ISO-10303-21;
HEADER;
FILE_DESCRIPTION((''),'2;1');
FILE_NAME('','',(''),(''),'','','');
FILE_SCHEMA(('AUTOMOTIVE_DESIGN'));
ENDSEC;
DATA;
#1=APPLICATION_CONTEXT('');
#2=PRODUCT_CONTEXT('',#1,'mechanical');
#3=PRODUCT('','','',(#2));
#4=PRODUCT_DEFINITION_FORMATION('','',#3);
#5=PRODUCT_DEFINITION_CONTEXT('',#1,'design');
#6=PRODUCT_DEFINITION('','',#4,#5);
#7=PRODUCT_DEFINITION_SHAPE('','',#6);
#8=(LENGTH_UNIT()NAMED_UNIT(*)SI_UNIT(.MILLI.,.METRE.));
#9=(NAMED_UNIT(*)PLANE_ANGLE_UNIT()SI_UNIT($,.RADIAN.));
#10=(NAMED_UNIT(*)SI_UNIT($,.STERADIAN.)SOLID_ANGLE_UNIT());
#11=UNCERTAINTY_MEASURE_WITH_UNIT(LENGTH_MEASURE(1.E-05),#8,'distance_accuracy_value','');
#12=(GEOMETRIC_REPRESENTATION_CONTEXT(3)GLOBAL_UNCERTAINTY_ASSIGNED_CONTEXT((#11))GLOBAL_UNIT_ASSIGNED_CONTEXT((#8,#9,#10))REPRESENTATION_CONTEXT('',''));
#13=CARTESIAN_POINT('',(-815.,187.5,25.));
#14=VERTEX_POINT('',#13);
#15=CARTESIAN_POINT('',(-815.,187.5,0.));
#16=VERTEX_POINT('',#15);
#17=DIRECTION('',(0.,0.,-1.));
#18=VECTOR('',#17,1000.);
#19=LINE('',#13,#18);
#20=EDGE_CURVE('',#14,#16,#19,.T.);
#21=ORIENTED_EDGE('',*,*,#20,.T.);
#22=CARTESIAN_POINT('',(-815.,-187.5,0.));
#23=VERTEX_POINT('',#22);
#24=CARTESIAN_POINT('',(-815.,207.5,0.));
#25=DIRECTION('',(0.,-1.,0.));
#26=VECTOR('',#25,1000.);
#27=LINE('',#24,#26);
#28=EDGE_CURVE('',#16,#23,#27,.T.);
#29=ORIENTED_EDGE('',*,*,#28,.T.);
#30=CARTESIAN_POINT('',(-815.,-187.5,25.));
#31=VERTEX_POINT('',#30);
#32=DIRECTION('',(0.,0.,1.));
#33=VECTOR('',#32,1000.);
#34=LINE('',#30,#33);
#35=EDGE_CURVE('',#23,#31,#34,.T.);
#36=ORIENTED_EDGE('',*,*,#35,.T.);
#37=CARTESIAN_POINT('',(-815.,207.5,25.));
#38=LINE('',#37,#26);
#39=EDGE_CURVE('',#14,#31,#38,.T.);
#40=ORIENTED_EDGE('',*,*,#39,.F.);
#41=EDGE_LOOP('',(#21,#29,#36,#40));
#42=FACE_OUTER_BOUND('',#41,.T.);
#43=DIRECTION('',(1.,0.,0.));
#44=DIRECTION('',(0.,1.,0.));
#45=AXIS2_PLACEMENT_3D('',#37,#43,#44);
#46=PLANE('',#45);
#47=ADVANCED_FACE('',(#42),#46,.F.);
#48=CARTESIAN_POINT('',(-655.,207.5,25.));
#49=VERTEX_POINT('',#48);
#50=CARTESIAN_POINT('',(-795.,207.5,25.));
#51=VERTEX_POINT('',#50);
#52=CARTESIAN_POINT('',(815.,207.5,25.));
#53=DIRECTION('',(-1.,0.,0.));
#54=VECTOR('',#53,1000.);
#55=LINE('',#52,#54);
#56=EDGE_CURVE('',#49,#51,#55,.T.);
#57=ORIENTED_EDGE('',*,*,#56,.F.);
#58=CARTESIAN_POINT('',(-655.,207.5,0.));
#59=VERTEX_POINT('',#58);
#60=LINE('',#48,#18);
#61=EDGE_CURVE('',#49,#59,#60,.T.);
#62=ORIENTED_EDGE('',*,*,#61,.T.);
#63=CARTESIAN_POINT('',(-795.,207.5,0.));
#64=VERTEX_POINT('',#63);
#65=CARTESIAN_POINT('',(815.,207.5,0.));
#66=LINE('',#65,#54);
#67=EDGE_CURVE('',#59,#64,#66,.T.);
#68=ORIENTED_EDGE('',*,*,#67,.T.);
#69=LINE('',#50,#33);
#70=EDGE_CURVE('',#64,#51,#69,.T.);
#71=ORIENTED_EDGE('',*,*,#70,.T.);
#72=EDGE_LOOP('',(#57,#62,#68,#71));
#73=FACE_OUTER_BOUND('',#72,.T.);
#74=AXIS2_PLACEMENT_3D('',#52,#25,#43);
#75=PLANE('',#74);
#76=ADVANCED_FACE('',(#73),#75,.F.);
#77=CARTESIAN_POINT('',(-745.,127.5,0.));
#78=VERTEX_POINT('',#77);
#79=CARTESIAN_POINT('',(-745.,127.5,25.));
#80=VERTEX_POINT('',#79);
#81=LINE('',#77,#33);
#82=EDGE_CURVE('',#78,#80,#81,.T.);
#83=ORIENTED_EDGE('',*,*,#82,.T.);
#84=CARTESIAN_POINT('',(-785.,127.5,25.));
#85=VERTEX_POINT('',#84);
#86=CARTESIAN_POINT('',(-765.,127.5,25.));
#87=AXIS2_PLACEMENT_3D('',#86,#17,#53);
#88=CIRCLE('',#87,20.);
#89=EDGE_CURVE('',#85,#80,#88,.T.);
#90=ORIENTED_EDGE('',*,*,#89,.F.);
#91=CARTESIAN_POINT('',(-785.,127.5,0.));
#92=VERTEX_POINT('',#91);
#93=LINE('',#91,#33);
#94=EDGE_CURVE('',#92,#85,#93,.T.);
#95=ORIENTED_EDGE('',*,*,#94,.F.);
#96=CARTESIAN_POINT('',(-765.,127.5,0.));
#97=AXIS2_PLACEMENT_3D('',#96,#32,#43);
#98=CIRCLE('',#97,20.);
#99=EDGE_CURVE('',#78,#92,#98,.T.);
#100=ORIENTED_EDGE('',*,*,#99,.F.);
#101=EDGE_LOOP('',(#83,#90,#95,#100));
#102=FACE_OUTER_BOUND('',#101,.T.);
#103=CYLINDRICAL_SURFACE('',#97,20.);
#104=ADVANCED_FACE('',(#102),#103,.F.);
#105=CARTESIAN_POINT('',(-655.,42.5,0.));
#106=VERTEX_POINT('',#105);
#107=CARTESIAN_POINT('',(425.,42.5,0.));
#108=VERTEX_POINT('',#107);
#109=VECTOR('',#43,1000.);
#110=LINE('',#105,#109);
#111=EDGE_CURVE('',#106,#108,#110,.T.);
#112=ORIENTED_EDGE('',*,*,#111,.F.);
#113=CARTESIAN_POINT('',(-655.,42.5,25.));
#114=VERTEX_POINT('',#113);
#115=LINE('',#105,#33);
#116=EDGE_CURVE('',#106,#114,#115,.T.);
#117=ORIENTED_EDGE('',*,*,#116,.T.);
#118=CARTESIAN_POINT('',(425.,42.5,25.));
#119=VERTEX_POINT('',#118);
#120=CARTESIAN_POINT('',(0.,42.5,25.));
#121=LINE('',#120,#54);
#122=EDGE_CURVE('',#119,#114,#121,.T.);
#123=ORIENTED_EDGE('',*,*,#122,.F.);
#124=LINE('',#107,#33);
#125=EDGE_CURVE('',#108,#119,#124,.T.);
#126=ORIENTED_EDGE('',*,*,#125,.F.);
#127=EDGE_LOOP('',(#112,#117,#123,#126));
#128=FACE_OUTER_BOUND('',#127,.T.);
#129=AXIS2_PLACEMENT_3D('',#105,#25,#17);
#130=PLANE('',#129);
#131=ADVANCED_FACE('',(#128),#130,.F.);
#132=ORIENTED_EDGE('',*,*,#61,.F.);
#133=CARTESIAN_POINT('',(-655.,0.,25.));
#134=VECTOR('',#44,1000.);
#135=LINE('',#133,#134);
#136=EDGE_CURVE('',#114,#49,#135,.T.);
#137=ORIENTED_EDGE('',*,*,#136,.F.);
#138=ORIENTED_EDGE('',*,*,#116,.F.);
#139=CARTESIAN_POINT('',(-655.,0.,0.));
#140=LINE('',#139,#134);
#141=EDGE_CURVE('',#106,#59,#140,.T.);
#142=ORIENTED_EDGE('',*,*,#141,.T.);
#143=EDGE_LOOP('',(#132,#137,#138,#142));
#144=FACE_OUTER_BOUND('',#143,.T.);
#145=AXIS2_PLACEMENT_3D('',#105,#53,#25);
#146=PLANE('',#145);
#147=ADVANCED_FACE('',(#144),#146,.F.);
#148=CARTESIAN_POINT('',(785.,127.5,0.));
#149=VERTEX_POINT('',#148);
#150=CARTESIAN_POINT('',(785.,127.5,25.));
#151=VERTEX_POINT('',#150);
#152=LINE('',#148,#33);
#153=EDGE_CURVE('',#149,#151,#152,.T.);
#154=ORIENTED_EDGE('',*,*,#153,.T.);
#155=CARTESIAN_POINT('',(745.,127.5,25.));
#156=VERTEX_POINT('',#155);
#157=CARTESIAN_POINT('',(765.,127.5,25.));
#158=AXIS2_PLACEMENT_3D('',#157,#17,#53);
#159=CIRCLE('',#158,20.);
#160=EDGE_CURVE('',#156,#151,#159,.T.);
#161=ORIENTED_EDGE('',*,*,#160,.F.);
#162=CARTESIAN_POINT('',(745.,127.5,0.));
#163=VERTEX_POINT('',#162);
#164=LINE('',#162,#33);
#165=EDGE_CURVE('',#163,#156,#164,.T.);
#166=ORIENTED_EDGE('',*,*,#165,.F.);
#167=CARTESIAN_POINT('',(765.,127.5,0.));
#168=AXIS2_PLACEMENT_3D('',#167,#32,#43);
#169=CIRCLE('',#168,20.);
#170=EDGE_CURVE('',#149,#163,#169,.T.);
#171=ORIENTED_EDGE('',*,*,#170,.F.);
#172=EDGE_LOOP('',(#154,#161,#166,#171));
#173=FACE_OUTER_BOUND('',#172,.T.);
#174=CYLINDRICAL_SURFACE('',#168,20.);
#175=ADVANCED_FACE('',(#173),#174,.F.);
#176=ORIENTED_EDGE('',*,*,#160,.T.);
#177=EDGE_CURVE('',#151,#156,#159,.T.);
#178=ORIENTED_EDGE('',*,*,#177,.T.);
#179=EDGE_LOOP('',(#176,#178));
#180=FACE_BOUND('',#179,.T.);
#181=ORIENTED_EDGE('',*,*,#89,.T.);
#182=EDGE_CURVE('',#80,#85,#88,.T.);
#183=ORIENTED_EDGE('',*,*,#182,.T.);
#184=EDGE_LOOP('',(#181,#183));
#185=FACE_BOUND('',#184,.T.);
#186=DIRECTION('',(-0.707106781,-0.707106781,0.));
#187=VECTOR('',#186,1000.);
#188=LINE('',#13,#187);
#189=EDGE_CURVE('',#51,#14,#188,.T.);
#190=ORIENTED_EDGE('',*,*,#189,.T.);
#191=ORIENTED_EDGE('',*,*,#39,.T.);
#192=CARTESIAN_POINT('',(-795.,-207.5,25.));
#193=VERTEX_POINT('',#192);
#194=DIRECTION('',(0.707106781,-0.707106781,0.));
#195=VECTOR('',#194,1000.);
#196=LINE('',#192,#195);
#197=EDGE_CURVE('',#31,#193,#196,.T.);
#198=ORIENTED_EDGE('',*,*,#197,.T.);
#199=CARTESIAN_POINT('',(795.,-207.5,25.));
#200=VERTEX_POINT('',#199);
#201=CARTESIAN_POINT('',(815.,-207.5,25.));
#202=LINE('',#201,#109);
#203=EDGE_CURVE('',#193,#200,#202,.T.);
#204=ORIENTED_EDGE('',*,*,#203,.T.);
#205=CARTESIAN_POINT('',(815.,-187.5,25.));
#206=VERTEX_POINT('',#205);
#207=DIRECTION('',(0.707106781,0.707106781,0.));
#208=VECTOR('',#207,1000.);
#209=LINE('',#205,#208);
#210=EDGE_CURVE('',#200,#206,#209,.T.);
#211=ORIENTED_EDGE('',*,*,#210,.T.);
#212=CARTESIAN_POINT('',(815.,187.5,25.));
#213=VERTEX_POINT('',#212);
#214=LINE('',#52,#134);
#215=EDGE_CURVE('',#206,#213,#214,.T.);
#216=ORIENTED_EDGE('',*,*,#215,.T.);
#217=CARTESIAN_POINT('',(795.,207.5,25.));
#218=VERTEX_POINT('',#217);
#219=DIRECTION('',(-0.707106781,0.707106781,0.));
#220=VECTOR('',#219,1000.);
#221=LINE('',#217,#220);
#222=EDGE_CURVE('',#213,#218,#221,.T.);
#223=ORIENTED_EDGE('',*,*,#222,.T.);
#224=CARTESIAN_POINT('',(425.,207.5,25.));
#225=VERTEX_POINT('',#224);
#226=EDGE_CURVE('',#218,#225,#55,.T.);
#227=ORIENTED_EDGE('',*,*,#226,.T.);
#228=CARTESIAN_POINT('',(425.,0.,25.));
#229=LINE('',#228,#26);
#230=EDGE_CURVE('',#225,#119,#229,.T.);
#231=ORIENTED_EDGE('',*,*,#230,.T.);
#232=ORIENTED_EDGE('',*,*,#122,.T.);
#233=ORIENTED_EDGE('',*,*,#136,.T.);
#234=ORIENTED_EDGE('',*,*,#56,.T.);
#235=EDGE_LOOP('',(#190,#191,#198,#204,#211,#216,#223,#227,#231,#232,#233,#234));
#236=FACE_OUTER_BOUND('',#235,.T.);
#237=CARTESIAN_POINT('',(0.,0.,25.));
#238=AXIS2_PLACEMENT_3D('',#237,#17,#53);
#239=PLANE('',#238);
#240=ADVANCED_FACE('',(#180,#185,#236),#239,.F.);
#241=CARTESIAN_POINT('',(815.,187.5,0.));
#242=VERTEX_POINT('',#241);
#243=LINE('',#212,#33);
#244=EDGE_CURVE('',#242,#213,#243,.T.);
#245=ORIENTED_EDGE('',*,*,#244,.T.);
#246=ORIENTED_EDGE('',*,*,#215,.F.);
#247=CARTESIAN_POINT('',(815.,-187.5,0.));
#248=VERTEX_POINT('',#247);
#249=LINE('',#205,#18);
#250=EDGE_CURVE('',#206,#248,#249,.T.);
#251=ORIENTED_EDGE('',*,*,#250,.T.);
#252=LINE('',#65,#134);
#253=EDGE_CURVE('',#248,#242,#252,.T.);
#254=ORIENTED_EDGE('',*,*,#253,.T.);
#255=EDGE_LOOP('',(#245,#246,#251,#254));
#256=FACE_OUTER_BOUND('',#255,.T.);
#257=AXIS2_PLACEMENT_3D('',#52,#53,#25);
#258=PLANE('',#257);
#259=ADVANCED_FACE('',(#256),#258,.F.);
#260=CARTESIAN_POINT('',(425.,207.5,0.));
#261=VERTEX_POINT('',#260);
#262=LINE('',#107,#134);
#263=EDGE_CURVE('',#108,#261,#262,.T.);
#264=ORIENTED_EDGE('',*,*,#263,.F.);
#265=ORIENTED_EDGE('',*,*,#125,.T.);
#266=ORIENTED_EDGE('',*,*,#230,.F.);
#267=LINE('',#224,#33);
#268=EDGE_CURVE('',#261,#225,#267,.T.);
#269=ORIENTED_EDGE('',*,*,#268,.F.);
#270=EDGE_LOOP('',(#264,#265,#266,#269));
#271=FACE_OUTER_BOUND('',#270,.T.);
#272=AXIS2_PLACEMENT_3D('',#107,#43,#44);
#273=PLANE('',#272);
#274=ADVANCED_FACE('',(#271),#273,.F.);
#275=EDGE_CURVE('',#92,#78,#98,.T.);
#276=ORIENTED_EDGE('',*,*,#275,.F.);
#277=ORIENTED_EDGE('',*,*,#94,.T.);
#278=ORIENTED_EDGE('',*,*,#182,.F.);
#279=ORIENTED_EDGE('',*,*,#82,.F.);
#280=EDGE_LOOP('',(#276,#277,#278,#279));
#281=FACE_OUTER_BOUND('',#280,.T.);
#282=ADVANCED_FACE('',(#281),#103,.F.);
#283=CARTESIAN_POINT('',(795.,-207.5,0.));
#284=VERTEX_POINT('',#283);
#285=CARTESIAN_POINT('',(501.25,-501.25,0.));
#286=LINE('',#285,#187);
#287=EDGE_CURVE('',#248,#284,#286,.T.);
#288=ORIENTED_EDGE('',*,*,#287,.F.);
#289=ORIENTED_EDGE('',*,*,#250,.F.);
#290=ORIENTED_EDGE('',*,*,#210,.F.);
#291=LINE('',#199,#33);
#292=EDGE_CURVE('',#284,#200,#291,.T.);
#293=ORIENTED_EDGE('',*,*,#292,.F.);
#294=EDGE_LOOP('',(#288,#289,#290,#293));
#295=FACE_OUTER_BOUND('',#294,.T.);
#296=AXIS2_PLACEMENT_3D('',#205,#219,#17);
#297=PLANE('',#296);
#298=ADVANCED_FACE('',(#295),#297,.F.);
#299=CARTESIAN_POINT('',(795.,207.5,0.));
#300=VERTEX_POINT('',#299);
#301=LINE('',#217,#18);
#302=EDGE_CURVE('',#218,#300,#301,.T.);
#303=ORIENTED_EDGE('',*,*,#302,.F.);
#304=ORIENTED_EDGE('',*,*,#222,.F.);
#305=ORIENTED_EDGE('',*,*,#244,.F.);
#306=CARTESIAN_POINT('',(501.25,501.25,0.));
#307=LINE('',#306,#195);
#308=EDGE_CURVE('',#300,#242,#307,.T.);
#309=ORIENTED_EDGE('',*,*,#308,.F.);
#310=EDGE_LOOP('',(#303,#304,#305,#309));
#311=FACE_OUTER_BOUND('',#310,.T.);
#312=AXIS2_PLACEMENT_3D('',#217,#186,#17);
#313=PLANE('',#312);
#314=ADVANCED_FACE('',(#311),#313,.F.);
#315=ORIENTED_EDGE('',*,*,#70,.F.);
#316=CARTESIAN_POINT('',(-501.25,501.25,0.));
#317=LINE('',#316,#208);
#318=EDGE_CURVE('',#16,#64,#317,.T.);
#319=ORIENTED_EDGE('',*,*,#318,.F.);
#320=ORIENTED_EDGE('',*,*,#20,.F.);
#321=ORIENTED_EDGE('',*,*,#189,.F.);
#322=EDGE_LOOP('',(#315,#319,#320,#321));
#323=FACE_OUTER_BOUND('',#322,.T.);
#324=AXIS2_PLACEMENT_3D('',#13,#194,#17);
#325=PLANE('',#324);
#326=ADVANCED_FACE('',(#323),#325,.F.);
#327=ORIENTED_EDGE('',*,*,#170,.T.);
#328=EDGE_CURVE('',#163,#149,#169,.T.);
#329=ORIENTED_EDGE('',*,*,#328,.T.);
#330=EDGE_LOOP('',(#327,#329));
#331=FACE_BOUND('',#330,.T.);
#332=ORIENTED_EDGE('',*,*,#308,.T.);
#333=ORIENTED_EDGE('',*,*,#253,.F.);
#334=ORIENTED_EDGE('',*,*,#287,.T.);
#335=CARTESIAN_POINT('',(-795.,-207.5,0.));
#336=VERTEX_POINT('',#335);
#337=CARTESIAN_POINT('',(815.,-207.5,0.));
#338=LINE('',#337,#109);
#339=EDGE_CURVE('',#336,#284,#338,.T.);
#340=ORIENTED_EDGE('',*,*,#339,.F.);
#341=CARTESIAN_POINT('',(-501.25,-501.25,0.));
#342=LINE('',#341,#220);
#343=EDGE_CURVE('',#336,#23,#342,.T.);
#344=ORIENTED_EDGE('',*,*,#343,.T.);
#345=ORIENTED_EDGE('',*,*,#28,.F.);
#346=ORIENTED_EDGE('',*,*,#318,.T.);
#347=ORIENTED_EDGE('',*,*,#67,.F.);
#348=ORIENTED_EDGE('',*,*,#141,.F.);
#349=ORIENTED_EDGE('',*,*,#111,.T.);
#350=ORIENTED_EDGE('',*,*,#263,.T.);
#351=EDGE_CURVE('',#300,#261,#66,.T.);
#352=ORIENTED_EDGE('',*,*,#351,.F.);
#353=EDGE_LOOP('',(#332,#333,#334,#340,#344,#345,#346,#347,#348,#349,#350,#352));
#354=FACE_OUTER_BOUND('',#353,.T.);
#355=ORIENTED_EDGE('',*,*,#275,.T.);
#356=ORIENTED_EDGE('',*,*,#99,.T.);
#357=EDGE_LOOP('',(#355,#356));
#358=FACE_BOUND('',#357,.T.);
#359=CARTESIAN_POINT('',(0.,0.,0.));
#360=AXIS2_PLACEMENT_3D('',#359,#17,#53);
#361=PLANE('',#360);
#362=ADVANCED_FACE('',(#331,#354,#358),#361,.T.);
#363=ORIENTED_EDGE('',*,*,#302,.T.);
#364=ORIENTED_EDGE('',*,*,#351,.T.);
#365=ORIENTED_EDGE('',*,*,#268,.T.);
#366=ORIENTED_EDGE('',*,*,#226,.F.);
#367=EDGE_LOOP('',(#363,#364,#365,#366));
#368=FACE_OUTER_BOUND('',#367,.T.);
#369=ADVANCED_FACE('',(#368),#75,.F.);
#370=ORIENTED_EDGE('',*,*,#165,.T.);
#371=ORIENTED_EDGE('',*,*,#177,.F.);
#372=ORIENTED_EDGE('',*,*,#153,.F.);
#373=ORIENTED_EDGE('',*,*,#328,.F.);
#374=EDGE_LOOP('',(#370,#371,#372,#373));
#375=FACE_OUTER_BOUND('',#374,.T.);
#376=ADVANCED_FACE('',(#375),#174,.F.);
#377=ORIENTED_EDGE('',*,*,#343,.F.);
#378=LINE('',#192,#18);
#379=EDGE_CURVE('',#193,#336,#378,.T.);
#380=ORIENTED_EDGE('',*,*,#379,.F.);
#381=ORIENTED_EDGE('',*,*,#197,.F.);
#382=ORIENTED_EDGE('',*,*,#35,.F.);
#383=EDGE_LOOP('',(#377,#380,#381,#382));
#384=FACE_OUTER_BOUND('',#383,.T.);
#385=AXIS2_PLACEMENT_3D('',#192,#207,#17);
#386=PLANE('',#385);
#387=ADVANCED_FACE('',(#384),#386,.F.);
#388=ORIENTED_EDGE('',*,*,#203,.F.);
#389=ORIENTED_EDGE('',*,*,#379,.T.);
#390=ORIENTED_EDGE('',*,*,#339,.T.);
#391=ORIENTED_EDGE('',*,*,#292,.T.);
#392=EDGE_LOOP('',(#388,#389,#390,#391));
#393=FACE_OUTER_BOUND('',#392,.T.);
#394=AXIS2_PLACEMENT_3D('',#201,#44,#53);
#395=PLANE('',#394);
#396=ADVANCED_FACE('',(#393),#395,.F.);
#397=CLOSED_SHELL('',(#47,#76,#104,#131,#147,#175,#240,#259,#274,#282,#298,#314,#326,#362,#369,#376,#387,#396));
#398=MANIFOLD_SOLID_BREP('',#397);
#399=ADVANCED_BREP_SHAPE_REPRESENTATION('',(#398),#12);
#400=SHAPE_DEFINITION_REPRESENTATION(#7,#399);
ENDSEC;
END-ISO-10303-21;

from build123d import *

# Parameters (mm, degrees)
SKETCH1_W               = 1630
SKETCH1_H               = 415
BOSS_EXTRUDE1_DEPTH     = 25
CHAMFER1_SIZE           = 20
CUT_EXTRUDE1_DEPTH      = 842.371647965
CUT_EXTRUDE1_DEPTH_BACK = 842.371647965
SKETCH2_R               = 20
SKETCH2_W               = 1080
SKETCH2_H               = 200


with BuildPart() as part:
    # Sketch1 → Boss-Extrude1 (new body)
    with BuildSketch(Plane.XY):
        Rectangle(SKETCH1_W, SKETCH1_H)
    extrude(amount=BOSS_EXTRUDE1_DEPTH)

    # Chamfer1
    chamfer1_edges = [part.edges().sort_by_distance(p)[0] for p in [
        (-815, 207.5, 12.5),
        (815, 207.5, 12.5),
        (815, -207.5, 12.5),
        (-815, -207.5, 12.5),
    ]]
    chamfer(chamfer1_edges, length=CHAMFER1_SIZE)

    # Sketch2 → Cut-Extrude1 (cut, two sides: drawn at the far end of the back side and taken through both)
    with BuildSketch(Plane.XY.offset(25).offset(-CUT_EXTRUDE1_DEPTH_BACK)):
        with Locations((-765, 127.5)):
            Circle(SKETCH2_R)
        with Locations((765, 127.5)):
            Circle(SKETCH2_R)
        with Locations((-115, 142.5)):
            Rectangle(SKETCH2_W, SKETCH2_H)
    extrude(amount=CUT_EXTRUDE1_DEPTH + CUT_EXTRUDE1_DEPTH_BACK, mode=Mode.SUBTRACT)


solid = part.part
